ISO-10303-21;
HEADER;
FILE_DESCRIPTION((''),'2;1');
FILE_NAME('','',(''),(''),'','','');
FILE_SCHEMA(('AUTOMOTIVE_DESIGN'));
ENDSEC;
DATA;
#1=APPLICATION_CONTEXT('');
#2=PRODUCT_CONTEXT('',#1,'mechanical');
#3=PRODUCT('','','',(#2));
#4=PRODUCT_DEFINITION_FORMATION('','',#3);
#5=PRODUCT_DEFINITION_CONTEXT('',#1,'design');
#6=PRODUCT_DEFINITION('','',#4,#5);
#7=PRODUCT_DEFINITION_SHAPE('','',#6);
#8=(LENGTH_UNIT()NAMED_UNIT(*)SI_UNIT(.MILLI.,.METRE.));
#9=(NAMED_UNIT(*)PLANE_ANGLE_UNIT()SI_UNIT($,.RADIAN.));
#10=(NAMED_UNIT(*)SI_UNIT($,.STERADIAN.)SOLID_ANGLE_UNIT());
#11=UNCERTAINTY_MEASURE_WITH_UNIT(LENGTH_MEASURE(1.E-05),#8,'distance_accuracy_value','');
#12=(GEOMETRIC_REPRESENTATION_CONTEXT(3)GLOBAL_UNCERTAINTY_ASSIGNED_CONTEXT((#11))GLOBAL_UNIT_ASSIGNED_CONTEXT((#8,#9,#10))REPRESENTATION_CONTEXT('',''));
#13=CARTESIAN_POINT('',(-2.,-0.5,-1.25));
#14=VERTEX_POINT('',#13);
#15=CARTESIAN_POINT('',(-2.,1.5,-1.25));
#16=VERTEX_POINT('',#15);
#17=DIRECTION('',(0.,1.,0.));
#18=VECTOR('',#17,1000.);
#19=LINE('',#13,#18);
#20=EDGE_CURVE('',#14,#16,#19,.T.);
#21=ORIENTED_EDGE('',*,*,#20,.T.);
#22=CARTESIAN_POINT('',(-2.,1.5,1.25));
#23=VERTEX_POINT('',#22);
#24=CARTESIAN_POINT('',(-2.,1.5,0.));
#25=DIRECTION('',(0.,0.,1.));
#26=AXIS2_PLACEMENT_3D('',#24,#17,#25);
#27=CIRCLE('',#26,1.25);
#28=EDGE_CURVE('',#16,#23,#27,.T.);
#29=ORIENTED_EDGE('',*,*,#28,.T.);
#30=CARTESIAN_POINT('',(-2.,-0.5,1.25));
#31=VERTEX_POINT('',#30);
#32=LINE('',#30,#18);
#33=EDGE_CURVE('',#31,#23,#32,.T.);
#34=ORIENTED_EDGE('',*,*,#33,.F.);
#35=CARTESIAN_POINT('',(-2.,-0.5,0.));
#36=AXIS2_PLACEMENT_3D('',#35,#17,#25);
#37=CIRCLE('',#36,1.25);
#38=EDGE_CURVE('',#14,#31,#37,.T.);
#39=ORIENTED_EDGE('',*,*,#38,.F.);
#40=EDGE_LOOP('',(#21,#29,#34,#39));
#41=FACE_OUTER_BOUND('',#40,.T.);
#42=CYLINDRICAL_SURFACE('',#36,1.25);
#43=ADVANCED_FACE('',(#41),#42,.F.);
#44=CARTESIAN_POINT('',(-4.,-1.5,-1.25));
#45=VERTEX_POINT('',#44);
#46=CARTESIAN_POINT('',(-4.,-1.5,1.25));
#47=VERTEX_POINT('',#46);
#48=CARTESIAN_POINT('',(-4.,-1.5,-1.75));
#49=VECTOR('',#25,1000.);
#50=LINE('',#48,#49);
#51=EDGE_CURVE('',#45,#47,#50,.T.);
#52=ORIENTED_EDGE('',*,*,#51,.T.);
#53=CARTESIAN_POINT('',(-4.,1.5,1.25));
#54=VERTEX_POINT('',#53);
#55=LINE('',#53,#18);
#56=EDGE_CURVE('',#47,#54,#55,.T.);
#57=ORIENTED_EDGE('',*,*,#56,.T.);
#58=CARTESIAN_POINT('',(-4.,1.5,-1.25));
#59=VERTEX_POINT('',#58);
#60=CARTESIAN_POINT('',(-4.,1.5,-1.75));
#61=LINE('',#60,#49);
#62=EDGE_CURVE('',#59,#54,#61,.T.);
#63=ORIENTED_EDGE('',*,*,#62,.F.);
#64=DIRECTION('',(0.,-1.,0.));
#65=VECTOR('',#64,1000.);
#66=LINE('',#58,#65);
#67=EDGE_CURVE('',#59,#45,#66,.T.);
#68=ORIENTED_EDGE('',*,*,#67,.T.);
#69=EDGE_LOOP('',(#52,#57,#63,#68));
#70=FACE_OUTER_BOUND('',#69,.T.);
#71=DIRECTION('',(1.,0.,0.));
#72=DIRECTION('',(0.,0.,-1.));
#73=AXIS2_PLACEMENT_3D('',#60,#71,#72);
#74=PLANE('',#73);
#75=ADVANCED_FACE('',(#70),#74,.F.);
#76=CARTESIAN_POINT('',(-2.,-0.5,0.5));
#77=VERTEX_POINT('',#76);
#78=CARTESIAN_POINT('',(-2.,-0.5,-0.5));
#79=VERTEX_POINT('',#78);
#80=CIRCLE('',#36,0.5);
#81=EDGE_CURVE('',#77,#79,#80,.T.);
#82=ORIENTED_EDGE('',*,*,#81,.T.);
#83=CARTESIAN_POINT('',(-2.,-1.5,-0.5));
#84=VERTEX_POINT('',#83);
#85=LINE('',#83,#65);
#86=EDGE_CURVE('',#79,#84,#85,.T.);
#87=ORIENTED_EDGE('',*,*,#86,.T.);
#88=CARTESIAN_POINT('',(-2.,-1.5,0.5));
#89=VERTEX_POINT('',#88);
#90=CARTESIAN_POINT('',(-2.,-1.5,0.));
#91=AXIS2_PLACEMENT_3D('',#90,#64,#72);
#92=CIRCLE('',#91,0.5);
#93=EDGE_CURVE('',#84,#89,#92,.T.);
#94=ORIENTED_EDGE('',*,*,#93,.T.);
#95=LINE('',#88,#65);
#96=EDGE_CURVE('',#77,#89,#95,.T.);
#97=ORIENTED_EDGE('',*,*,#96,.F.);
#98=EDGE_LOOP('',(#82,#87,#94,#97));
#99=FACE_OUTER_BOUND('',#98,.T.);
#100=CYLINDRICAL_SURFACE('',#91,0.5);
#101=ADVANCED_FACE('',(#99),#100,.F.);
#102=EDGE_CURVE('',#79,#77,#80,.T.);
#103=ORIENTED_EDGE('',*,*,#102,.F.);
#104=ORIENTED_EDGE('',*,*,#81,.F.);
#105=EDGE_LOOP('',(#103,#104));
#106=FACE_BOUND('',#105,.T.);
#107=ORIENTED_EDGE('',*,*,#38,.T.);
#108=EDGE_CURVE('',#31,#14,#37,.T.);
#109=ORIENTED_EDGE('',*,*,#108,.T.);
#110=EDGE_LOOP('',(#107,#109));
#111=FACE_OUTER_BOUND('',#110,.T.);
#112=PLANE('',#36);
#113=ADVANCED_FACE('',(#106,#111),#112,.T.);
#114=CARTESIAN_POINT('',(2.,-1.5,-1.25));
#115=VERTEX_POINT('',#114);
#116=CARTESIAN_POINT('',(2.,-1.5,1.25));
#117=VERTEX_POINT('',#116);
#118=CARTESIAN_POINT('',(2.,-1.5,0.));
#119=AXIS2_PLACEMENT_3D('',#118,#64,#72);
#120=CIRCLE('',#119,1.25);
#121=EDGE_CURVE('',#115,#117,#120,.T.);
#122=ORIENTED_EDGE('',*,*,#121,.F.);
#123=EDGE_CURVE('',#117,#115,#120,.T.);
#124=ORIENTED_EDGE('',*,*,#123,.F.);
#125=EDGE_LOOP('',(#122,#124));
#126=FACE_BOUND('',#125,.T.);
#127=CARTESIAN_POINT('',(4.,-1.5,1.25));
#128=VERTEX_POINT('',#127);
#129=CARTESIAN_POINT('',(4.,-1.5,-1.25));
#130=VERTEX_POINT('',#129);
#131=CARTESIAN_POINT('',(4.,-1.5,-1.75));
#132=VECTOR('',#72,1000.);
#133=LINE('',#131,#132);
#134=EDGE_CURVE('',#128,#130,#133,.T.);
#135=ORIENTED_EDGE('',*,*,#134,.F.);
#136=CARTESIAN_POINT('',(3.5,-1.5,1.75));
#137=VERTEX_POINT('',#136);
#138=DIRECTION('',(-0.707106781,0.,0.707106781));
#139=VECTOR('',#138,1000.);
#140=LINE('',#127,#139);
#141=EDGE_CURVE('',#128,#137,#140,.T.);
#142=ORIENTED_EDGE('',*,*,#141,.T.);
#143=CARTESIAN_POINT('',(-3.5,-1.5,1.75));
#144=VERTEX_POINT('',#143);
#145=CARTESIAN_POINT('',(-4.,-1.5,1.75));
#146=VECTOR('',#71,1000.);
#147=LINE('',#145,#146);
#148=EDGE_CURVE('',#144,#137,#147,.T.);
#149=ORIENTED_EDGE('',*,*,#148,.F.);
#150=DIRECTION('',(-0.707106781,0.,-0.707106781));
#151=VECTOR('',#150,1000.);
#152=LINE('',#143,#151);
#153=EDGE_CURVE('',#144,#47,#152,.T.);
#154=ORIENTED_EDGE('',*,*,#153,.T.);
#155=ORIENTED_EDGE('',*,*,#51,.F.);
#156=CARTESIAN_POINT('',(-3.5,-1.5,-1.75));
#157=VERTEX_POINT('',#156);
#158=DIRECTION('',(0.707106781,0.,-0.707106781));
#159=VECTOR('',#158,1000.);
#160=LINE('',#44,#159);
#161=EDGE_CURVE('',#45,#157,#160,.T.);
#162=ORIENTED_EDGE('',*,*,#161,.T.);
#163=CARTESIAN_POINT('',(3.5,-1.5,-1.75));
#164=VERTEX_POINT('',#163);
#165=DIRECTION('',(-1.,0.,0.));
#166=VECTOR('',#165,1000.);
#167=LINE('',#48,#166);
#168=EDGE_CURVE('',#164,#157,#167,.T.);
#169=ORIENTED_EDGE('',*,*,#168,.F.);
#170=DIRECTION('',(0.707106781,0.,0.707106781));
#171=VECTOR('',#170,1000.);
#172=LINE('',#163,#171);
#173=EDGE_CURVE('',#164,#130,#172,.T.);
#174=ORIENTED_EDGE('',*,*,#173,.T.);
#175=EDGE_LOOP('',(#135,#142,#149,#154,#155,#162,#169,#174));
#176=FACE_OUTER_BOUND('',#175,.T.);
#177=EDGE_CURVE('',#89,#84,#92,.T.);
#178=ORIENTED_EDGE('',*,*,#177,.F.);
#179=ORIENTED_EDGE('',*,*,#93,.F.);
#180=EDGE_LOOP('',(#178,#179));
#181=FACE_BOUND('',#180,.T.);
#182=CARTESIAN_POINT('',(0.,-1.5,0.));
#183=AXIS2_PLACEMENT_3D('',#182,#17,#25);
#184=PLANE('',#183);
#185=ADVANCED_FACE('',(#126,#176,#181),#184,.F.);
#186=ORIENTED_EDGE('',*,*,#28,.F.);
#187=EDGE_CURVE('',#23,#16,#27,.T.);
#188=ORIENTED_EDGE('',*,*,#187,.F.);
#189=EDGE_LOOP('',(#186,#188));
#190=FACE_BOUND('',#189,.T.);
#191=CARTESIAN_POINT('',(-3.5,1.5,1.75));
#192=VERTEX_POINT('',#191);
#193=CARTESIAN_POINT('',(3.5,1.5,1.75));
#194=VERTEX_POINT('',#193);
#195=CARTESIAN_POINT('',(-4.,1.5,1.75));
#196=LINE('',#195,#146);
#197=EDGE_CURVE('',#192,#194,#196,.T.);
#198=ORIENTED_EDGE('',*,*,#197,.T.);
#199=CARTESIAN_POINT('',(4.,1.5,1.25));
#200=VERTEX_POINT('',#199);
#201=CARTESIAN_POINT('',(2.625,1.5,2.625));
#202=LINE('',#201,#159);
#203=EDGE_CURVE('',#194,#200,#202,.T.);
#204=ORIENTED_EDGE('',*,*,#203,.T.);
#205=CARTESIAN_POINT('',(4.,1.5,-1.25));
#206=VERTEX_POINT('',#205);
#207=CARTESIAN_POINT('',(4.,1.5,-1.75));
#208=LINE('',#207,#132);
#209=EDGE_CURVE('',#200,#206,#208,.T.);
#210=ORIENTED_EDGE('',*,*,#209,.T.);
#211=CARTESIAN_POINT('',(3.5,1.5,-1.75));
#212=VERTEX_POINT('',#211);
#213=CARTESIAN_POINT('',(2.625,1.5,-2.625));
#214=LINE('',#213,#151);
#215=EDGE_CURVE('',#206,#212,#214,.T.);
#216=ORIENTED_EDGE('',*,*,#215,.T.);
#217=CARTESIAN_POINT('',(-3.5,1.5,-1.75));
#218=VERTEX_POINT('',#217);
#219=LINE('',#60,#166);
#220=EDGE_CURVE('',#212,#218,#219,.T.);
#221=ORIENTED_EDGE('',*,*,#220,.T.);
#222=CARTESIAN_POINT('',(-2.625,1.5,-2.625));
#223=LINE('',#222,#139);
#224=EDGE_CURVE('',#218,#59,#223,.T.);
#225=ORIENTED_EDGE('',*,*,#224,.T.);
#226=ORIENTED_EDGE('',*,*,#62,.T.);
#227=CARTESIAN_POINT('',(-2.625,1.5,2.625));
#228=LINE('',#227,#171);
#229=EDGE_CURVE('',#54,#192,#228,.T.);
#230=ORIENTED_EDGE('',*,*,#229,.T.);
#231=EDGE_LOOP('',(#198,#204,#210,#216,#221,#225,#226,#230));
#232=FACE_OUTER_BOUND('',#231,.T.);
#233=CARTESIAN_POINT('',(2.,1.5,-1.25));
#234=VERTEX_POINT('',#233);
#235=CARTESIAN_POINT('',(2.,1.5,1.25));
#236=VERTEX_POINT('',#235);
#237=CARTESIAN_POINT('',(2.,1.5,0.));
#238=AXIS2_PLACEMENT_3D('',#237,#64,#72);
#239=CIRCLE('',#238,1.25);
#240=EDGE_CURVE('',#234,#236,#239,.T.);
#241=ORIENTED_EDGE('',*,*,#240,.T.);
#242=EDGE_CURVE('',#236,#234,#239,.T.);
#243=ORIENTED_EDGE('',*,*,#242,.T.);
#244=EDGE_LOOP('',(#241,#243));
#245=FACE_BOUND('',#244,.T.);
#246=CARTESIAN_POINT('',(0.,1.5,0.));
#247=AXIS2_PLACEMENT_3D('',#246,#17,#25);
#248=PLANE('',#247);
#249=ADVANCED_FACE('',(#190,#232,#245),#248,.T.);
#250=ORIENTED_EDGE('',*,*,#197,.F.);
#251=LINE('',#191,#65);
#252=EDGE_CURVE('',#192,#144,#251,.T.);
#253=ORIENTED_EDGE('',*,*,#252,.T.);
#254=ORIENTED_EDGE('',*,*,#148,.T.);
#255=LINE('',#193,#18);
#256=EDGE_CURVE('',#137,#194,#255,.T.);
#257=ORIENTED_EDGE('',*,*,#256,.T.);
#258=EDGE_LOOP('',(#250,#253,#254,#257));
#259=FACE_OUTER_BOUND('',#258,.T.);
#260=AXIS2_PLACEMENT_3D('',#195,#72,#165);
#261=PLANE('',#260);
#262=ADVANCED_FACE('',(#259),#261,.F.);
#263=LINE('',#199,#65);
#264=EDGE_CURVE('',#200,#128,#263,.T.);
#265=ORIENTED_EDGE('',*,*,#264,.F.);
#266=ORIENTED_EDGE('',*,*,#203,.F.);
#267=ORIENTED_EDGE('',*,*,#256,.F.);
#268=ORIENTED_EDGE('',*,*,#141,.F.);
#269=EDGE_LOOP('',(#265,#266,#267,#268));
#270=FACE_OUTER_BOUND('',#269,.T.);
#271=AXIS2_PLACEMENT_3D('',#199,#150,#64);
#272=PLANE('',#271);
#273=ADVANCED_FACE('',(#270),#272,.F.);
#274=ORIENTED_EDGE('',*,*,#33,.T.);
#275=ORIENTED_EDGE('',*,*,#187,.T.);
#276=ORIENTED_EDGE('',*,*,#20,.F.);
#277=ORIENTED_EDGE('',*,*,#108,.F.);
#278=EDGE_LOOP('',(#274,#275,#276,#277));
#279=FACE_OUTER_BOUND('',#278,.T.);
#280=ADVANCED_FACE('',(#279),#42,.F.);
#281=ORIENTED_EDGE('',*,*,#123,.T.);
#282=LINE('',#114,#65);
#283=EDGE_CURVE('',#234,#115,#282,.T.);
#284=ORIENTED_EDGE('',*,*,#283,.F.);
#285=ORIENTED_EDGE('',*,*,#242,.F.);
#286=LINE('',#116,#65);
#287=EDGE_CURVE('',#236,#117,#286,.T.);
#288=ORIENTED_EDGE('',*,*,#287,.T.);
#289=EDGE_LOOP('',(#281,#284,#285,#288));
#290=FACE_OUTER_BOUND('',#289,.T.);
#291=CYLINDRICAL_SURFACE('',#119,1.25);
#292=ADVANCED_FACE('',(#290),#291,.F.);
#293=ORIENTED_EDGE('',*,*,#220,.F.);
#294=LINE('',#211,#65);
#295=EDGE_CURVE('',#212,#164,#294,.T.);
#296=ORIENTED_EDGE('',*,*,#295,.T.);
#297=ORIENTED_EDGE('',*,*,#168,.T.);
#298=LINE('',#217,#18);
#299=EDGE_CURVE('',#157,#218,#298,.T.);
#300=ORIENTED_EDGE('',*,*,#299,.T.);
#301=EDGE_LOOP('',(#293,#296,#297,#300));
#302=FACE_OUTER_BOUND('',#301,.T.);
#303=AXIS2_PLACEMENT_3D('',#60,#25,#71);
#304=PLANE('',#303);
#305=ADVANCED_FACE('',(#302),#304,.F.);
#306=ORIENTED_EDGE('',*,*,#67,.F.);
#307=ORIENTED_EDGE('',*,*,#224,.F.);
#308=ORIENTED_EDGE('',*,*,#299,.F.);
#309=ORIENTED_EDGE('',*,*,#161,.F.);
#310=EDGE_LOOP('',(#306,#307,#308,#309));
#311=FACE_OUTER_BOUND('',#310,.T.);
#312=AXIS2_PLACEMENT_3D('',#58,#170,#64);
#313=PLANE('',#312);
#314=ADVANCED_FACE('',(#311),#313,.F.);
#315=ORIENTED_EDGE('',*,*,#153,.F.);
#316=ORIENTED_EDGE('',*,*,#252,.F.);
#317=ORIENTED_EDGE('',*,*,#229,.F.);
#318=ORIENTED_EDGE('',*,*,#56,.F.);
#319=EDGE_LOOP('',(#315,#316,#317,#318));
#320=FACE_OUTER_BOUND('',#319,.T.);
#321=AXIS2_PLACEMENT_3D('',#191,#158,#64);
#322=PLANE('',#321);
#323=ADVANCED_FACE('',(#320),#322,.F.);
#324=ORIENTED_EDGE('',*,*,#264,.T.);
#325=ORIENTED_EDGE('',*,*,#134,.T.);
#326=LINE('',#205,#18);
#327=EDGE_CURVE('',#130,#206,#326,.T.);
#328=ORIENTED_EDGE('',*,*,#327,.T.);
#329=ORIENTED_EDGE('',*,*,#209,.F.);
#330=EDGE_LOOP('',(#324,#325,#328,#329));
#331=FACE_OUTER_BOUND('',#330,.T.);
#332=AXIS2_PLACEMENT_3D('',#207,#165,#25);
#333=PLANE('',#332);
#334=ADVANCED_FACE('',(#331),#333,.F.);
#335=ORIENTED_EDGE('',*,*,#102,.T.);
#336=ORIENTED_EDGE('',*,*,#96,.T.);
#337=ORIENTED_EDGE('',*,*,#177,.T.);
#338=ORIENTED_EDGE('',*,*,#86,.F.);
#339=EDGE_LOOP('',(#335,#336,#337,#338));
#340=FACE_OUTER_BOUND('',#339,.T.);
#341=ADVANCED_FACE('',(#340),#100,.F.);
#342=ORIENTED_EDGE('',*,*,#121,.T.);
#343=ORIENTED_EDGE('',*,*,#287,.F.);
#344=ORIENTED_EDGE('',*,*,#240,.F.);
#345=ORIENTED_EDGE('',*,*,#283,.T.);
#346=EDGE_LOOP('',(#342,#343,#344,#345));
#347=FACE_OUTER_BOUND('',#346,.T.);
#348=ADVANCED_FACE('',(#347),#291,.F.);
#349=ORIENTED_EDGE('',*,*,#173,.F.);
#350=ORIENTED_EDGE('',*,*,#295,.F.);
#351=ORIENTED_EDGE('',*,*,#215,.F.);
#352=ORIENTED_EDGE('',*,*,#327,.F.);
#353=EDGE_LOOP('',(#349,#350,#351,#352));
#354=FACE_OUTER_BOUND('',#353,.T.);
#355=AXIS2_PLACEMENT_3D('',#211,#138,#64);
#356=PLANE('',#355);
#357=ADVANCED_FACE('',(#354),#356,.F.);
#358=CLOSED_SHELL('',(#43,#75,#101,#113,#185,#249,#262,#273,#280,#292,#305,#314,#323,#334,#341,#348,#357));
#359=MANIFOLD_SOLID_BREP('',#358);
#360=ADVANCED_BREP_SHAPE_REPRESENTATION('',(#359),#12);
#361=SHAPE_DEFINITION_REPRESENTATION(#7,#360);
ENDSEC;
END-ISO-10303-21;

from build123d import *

# Parameters (mm, degrees)
SKETCH1_W                  = 8
SKETCH1_H                  = 3.5
BOSS_EXTRUDE1_DEPTH        = 1.5
SKETCH2_R                  = 1.25
CUT_EXTRUDE1_DEPTH         = 2
CHAMFER1_SIZE              = 0.5
F_1_0_1_DIAMETER_HOLE1_D   = 1
F_2_5_2_5_DIAMETER_HOLE1_D = 2.5


with BuildPart() as part:
    # Sketch1 → Boss-Extrude1 (new, symmetric)
    with BuildSketch(Plane(origin=(0, 0, 0), x_dir=(1, 0, 0), z_dir=(0, 1, 0))):
        Rectangle(SKETCH1_W, SKETCH1_H)
    extrude(amount=BOSS_EXTRUDE1_DEPTH, both=True)

    # Sketch2 → Cut-Extrude1 (cut)
    with BuildSketch(Plane(origin=(0, 1.5, 0), x_dir=(1, 0, 0), z_dir=(0, 1, 0))):
        with Locations(Location((-2, 0, 0), (0, 0, 270))):
            Circle(SKETCH2_R)
    extrude(amount=-CUT_EXTRUDE1_DEPTH, mode=Mode.SUBTRACT)

    # Chamfer1
    chamfer1_edges = [part.edges().sort_by_distance(p)[0] for p in [
        (4, 0, 1.75),
        (-4, 0, 1.75),
        (-4, 0, -1.75),
        (4, 0, -1.75),
    ]]
    chamfer(chamfer1_edges, length=CHAMFER1_SIZE)

    # Ø1.0 (1) Diameter Hole1 (through all)
    with Locations(Plane(origin=(0, -1.5, 0), x_dir=(-1, 0, 0), z_dir=(0, -1, 0))):
        with Locations((2, 0)):
            Hole(F_1_0_1_DIAMETER_HOLE1_D / 2)

    # Ø2.5 (2.5) Diameter Hole1 (through all)
    with Locations(Plane(origin=(0, -1.5, 0), x_dir=(-1, 0, 0), z_dir=(0, -1, 0))):
        with Locations((-2, 0)):
            Hole(F_2_5_2_5_DIAMETER_HOLE1_D / 2)


solid = part.part
